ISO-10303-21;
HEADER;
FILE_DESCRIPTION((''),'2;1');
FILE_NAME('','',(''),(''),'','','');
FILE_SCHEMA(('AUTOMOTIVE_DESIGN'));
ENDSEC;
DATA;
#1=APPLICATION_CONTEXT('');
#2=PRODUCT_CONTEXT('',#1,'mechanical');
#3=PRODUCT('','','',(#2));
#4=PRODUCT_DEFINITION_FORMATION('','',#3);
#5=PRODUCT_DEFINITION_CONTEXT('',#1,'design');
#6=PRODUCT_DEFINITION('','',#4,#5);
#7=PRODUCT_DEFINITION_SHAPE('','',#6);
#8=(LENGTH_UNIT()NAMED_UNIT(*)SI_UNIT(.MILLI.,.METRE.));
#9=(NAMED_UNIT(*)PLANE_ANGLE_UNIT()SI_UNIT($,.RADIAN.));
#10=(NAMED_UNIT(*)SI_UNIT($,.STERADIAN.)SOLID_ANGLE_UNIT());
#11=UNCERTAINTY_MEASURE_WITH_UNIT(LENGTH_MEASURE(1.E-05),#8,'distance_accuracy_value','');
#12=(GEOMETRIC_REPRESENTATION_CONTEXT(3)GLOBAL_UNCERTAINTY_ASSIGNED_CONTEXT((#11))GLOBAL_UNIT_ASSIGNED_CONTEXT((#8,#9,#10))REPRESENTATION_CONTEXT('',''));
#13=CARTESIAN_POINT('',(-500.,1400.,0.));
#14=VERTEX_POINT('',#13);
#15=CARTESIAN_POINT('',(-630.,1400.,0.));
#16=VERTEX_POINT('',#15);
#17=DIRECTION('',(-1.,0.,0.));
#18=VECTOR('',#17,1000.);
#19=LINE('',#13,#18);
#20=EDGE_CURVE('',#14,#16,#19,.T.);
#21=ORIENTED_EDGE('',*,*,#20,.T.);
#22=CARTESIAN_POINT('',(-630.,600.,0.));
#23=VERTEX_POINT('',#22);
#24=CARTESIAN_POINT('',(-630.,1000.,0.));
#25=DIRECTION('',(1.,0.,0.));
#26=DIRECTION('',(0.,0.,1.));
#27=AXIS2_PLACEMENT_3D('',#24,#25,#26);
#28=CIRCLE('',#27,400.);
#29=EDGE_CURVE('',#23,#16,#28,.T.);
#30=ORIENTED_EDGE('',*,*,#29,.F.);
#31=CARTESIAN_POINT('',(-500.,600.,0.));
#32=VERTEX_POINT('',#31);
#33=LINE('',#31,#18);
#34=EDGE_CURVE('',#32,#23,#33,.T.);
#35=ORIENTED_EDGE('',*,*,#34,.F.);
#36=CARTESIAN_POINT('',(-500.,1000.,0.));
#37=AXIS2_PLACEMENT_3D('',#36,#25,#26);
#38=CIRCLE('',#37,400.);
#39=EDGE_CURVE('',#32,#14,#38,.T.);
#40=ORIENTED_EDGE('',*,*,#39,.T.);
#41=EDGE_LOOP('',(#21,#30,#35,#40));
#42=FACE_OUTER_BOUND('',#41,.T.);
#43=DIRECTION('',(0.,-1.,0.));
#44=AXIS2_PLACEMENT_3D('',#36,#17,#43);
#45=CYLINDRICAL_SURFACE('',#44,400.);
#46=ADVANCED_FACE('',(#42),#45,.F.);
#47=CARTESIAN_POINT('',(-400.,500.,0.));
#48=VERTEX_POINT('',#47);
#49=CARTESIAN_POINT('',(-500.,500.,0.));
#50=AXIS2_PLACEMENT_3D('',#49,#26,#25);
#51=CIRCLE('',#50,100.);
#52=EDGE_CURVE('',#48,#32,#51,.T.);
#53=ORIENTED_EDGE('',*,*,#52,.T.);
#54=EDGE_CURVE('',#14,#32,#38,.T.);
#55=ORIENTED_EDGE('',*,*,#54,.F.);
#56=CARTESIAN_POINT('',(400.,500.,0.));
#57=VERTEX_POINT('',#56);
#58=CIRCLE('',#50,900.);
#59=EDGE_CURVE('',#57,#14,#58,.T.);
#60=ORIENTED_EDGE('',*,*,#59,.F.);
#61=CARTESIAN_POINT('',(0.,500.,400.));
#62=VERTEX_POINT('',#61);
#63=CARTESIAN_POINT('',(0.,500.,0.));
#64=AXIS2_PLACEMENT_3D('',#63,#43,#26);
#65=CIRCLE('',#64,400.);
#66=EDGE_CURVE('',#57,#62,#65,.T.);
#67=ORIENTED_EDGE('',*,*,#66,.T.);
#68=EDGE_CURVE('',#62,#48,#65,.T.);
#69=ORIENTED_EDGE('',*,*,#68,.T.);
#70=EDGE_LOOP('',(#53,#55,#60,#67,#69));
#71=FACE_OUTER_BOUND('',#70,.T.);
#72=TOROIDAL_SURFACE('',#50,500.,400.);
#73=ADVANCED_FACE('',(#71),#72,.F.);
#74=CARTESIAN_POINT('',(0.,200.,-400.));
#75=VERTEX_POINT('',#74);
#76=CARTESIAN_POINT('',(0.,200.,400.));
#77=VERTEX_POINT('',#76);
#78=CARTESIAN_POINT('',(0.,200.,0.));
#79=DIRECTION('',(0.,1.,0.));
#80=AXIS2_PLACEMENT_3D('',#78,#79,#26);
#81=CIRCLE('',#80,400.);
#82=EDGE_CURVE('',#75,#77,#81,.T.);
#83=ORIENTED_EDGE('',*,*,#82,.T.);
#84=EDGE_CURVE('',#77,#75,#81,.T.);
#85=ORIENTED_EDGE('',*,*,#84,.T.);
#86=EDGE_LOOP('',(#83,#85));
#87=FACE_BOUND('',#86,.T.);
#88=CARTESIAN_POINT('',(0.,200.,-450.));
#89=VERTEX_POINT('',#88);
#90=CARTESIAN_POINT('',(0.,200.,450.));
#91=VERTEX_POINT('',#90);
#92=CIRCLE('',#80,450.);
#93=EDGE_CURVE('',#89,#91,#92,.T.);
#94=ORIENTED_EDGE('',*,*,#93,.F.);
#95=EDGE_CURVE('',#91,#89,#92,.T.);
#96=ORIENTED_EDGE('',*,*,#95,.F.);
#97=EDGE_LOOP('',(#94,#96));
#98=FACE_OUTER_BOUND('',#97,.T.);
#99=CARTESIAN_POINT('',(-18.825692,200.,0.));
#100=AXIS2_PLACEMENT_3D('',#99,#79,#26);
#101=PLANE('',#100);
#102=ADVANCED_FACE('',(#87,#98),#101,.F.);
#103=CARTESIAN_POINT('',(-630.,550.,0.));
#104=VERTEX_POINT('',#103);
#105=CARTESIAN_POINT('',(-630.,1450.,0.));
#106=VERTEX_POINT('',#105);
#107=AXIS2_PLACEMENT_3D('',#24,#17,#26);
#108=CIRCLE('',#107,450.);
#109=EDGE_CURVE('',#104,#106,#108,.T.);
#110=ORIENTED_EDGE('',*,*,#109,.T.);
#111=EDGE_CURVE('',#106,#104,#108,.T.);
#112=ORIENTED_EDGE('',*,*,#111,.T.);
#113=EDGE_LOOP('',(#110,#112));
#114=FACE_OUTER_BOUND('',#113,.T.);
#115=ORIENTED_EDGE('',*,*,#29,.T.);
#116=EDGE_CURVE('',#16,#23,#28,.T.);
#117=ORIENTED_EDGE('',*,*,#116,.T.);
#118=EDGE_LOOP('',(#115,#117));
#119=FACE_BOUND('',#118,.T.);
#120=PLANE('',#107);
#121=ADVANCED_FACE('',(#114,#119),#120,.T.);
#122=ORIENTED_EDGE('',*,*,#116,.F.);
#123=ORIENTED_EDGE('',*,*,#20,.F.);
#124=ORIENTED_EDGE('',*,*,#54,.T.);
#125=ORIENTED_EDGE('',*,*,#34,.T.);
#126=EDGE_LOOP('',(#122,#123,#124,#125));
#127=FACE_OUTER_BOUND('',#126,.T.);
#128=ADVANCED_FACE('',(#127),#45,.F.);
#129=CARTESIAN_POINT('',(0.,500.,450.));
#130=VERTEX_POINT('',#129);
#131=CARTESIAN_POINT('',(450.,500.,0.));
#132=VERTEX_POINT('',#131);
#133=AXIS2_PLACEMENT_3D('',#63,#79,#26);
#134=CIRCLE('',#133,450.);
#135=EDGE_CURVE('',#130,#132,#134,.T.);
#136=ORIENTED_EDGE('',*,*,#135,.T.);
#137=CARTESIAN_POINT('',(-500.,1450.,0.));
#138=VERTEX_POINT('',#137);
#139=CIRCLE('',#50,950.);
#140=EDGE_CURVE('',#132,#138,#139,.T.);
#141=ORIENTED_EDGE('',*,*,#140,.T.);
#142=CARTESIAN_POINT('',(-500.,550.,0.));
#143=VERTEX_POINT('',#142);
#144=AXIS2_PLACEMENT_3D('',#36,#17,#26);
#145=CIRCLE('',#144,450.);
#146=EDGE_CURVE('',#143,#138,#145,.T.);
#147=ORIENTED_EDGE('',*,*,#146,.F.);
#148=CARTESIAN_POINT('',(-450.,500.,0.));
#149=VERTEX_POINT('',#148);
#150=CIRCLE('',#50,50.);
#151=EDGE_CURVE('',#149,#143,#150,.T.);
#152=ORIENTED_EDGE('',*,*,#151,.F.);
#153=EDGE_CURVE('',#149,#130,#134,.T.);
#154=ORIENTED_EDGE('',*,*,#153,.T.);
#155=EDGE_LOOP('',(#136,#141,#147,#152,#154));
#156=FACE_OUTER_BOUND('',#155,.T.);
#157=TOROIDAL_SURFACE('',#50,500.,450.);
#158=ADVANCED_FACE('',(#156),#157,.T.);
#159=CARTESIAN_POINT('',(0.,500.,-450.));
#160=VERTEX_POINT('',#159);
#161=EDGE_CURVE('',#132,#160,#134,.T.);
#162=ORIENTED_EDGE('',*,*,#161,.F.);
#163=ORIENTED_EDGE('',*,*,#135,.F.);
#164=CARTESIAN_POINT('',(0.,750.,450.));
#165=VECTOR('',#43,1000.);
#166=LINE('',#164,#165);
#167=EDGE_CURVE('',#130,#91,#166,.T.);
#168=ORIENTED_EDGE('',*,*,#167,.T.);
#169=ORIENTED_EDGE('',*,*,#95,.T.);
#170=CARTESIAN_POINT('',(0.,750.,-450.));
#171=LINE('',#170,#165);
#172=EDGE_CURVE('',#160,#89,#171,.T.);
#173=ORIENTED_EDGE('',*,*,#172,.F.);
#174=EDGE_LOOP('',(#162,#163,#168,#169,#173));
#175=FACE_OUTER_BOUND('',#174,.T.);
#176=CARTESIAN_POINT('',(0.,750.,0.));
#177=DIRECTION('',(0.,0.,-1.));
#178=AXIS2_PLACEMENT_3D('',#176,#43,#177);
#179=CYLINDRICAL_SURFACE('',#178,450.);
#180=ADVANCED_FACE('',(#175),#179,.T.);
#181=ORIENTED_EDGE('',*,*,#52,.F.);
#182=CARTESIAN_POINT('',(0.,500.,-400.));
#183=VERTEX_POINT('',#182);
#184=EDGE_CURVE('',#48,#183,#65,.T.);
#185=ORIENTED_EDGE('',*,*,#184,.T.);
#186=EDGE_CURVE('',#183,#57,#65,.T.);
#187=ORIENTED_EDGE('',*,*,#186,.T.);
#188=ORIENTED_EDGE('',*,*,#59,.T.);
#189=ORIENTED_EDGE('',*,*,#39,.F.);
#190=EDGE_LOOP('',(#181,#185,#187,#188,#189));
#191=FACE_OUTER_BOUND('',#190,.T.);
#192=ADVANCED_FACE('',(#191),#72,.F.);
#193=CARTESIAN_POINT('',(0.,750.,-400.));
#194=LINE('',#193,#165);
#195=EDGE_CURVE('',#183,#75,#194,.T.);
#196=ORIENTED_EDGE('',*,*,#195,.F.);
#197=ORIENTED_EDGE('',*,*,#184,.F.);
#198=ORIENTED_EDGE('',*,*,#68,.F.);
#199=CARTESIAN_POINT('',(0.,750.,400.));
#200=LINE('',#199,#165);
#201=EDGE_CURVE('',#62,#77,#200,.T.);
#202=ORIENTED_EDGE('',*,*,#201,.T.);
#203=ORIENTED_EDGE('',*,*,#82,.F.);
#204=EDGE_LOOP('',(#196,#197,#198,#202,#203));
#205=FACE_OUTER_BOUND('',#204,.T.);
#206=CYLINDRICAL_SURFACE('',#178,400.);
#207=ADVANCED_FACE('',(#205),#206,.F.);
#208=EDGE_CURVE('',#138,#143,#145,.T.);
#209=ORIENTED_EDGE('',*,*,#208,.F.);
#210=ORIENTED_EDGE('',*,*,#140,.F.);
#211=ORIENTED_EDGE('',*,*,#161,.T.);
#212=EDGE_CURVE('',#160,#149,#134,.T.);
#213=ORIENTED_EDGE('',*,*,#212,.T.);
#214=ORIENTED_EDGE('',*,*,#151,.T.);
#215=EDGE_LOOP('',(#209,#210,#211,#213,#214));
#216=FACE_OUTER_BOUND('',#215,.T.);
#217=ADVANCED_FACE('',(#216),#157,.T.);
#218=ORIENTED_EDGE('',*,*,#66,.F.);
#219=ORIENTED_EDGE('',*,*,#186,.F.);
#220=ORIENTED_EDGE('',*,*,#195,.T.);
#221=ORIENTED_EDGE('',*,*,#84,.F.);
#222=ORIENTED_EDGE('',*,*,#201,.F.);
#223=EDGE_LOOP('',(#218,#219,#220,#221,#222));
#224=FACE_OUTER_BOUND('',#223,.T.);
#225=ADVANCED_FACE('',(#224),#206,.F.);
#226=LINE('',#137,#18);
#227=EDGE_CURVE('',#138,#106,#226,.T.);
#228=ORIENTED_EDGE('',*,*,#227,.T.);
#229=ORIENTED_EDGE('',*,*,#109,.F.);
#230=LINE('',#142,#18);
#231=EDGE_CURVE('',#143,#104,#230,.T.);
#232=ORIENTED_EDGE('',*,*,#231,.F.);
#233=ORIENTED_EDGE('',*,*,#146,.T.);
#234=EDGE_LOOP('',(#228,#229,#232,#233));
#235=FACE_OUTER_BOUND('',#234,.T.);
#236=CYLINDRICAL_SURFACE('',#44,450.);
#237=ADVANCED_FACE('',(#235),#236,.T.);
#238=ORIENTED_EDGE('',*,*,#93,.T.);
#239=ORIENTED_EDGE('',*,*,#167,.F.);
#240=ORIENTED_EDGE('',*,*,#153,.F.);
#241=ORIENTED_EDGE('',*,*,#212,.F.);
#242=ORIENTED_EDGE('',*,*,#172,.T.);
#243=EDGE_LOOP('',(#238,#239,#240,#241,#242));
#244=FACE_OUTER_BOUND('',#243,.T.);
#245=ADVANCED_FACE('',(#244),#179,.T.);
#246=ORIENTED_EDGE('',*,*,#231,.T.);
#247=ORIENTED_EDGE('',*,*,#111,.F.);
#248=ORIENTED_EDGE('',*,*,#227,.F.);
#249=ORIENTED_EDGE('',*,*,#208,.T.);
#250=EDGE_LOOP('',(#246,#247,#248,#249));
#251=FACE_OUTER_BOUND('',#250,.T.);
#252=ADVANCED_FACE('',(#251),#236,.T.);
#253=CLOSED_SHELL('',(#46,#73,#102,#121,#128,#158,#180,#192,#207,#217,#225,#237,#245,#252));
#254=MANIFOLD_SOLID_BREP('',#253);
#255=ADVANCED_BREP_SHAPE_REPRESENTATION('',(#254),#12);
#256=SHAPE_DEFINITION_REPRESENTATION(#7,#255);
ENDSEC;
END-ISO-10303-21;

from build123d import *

# Parameters (mm, degrees)
SKETCH1_R           = 450
SKETCH1_R_2         = 400
BOSS_EXTRUDE1_DEPTH = 750
SKETCH2_R           = 650
BOSS_EXTRUDE2_DEPTH = 100
SKETCH3_R           = 50
CUT_EXTRUDE1_DEPTH  = 1846.264208725
MOVE_FACE1_BY       = 750
SKETCH9_R           = 450
SKETCH9_R_2         = 400
SKETCH11_R          = 1265.740496662
CUT_EXTRUDE2_DEPTH  = 3153
MOVE_FACE2_BY       = 370
MOVE_FACE3_BY       = 200


with BuildPart() as part:
    # Sketch1 → Boss-Extrude1 (new, symmetric)
    with BuildSketch(Plane(origin=(0, 0, 0), x_dir=(1, 0, 0), z_dir=(0, 1, 0))):
        with Locations(Location((0, 0, 0), (0, 0, 270))):
            Circle(SKETCH1_R)
        with Locations(Location((0, 0, 0), (0, 0, 270))):
            Circle(SKETCH1_R_2, mode=Mode.SUBTRACT)
    extrude(amount=BOSS_EXTRUDE1_DEPTH, both=True)

    # Sketch2 → Boss-Extrude2 (add)
    with BuildSketch(Plane.XZ.offset(750)):
        with Locations(Location((0, 0, 0), (0, 0, 270))):
            Circle(SKETCH2_R)
    extrude(amount=BOSS_EXTRUDE2_DEPTH)

    # Sketch3 → Cut-Extrude1 (cut, through all)
    with BuildSketch(Plane.XZ.offset(850)):
        with Locations(Location((0, 550, 0), (0, 0, 270))):
            Circle(SKETCH3_R)
        with Locations(Location((550, 0, 0), (0, 0, 270))):
            Circle(SKETCH3_R)
        with Locations(Location((0, -550, 0), (0, 0, 270))):
            Circle(SKETCH3_R)
        with Locations(Location((-550, 0, 0), (0, 0, 270))):
            Circle(SKETCH3_R)
    extrude(amount=-CUT_EXTRUDE1_DEPTH, mode=Mode.SUBTRACT)

    # Move Face1: a face moved inward by 750.0
    extrude(part.faces().sort_by_distance((-225, 750, 360))[0], amount=MOVE_FACE1_BY, dir=(0, -1, 0), mode=Mode.SUBTRACT)

    # Sweep1: sweep along a path in Sketch8
    with BuildLine(Plane.XY) as sweep1_path:
        Line((0, 0), (0, 500))
        ThreePointArc((0, 500), (-146.446609407, 853.553390593), (-500, 1000))
        Line((-500, 1000), (-1000, 1000))
    # Sketch9 → Sweep1 (sweep)
    with BuildSketch(Plane(origin=(0, 0, 0), x_dir=(1, 0, 0), z_dir=(0, 1, 0))):
        Circle(SKETCH9_R)
        Circle(SKETCH9_R_2, mode=Mode.SUBTRACT)
    sweep(path=sweep1_path.line)

    # Sketch11 → Cut-Extrude2 (cut)
    with BuildSketch(Plane(origin=(0, 0, 0), x_dir=(1, 0, 0), z_dir=(0, 1, 0))):
        with Locations((-18.825691705, 0)):
            Circle(SKETCH11_R)
    extrude(amount=-CUT_EXTRUDE2_DEPTH, mode=Mode.SUBTRACT)

    # Move Face2: a face moved inward by 370.0
    extrude(part.faces().sort_by_distance((-1000, 1360, 225))[0], amount=MOVE_FACE2_BY, dir=(1, 0, 0), mode=Mode.SUBTRACT)

    # Move Face3: a face moved inward by 200.0
    extrude(part.faces().sort_by_distance((-225, 0, 360))[0], amount=MOVE_FACE3_BY, dir=(0, 1, 0), mode=Mode.SUBTRACT)


solid = part.part
